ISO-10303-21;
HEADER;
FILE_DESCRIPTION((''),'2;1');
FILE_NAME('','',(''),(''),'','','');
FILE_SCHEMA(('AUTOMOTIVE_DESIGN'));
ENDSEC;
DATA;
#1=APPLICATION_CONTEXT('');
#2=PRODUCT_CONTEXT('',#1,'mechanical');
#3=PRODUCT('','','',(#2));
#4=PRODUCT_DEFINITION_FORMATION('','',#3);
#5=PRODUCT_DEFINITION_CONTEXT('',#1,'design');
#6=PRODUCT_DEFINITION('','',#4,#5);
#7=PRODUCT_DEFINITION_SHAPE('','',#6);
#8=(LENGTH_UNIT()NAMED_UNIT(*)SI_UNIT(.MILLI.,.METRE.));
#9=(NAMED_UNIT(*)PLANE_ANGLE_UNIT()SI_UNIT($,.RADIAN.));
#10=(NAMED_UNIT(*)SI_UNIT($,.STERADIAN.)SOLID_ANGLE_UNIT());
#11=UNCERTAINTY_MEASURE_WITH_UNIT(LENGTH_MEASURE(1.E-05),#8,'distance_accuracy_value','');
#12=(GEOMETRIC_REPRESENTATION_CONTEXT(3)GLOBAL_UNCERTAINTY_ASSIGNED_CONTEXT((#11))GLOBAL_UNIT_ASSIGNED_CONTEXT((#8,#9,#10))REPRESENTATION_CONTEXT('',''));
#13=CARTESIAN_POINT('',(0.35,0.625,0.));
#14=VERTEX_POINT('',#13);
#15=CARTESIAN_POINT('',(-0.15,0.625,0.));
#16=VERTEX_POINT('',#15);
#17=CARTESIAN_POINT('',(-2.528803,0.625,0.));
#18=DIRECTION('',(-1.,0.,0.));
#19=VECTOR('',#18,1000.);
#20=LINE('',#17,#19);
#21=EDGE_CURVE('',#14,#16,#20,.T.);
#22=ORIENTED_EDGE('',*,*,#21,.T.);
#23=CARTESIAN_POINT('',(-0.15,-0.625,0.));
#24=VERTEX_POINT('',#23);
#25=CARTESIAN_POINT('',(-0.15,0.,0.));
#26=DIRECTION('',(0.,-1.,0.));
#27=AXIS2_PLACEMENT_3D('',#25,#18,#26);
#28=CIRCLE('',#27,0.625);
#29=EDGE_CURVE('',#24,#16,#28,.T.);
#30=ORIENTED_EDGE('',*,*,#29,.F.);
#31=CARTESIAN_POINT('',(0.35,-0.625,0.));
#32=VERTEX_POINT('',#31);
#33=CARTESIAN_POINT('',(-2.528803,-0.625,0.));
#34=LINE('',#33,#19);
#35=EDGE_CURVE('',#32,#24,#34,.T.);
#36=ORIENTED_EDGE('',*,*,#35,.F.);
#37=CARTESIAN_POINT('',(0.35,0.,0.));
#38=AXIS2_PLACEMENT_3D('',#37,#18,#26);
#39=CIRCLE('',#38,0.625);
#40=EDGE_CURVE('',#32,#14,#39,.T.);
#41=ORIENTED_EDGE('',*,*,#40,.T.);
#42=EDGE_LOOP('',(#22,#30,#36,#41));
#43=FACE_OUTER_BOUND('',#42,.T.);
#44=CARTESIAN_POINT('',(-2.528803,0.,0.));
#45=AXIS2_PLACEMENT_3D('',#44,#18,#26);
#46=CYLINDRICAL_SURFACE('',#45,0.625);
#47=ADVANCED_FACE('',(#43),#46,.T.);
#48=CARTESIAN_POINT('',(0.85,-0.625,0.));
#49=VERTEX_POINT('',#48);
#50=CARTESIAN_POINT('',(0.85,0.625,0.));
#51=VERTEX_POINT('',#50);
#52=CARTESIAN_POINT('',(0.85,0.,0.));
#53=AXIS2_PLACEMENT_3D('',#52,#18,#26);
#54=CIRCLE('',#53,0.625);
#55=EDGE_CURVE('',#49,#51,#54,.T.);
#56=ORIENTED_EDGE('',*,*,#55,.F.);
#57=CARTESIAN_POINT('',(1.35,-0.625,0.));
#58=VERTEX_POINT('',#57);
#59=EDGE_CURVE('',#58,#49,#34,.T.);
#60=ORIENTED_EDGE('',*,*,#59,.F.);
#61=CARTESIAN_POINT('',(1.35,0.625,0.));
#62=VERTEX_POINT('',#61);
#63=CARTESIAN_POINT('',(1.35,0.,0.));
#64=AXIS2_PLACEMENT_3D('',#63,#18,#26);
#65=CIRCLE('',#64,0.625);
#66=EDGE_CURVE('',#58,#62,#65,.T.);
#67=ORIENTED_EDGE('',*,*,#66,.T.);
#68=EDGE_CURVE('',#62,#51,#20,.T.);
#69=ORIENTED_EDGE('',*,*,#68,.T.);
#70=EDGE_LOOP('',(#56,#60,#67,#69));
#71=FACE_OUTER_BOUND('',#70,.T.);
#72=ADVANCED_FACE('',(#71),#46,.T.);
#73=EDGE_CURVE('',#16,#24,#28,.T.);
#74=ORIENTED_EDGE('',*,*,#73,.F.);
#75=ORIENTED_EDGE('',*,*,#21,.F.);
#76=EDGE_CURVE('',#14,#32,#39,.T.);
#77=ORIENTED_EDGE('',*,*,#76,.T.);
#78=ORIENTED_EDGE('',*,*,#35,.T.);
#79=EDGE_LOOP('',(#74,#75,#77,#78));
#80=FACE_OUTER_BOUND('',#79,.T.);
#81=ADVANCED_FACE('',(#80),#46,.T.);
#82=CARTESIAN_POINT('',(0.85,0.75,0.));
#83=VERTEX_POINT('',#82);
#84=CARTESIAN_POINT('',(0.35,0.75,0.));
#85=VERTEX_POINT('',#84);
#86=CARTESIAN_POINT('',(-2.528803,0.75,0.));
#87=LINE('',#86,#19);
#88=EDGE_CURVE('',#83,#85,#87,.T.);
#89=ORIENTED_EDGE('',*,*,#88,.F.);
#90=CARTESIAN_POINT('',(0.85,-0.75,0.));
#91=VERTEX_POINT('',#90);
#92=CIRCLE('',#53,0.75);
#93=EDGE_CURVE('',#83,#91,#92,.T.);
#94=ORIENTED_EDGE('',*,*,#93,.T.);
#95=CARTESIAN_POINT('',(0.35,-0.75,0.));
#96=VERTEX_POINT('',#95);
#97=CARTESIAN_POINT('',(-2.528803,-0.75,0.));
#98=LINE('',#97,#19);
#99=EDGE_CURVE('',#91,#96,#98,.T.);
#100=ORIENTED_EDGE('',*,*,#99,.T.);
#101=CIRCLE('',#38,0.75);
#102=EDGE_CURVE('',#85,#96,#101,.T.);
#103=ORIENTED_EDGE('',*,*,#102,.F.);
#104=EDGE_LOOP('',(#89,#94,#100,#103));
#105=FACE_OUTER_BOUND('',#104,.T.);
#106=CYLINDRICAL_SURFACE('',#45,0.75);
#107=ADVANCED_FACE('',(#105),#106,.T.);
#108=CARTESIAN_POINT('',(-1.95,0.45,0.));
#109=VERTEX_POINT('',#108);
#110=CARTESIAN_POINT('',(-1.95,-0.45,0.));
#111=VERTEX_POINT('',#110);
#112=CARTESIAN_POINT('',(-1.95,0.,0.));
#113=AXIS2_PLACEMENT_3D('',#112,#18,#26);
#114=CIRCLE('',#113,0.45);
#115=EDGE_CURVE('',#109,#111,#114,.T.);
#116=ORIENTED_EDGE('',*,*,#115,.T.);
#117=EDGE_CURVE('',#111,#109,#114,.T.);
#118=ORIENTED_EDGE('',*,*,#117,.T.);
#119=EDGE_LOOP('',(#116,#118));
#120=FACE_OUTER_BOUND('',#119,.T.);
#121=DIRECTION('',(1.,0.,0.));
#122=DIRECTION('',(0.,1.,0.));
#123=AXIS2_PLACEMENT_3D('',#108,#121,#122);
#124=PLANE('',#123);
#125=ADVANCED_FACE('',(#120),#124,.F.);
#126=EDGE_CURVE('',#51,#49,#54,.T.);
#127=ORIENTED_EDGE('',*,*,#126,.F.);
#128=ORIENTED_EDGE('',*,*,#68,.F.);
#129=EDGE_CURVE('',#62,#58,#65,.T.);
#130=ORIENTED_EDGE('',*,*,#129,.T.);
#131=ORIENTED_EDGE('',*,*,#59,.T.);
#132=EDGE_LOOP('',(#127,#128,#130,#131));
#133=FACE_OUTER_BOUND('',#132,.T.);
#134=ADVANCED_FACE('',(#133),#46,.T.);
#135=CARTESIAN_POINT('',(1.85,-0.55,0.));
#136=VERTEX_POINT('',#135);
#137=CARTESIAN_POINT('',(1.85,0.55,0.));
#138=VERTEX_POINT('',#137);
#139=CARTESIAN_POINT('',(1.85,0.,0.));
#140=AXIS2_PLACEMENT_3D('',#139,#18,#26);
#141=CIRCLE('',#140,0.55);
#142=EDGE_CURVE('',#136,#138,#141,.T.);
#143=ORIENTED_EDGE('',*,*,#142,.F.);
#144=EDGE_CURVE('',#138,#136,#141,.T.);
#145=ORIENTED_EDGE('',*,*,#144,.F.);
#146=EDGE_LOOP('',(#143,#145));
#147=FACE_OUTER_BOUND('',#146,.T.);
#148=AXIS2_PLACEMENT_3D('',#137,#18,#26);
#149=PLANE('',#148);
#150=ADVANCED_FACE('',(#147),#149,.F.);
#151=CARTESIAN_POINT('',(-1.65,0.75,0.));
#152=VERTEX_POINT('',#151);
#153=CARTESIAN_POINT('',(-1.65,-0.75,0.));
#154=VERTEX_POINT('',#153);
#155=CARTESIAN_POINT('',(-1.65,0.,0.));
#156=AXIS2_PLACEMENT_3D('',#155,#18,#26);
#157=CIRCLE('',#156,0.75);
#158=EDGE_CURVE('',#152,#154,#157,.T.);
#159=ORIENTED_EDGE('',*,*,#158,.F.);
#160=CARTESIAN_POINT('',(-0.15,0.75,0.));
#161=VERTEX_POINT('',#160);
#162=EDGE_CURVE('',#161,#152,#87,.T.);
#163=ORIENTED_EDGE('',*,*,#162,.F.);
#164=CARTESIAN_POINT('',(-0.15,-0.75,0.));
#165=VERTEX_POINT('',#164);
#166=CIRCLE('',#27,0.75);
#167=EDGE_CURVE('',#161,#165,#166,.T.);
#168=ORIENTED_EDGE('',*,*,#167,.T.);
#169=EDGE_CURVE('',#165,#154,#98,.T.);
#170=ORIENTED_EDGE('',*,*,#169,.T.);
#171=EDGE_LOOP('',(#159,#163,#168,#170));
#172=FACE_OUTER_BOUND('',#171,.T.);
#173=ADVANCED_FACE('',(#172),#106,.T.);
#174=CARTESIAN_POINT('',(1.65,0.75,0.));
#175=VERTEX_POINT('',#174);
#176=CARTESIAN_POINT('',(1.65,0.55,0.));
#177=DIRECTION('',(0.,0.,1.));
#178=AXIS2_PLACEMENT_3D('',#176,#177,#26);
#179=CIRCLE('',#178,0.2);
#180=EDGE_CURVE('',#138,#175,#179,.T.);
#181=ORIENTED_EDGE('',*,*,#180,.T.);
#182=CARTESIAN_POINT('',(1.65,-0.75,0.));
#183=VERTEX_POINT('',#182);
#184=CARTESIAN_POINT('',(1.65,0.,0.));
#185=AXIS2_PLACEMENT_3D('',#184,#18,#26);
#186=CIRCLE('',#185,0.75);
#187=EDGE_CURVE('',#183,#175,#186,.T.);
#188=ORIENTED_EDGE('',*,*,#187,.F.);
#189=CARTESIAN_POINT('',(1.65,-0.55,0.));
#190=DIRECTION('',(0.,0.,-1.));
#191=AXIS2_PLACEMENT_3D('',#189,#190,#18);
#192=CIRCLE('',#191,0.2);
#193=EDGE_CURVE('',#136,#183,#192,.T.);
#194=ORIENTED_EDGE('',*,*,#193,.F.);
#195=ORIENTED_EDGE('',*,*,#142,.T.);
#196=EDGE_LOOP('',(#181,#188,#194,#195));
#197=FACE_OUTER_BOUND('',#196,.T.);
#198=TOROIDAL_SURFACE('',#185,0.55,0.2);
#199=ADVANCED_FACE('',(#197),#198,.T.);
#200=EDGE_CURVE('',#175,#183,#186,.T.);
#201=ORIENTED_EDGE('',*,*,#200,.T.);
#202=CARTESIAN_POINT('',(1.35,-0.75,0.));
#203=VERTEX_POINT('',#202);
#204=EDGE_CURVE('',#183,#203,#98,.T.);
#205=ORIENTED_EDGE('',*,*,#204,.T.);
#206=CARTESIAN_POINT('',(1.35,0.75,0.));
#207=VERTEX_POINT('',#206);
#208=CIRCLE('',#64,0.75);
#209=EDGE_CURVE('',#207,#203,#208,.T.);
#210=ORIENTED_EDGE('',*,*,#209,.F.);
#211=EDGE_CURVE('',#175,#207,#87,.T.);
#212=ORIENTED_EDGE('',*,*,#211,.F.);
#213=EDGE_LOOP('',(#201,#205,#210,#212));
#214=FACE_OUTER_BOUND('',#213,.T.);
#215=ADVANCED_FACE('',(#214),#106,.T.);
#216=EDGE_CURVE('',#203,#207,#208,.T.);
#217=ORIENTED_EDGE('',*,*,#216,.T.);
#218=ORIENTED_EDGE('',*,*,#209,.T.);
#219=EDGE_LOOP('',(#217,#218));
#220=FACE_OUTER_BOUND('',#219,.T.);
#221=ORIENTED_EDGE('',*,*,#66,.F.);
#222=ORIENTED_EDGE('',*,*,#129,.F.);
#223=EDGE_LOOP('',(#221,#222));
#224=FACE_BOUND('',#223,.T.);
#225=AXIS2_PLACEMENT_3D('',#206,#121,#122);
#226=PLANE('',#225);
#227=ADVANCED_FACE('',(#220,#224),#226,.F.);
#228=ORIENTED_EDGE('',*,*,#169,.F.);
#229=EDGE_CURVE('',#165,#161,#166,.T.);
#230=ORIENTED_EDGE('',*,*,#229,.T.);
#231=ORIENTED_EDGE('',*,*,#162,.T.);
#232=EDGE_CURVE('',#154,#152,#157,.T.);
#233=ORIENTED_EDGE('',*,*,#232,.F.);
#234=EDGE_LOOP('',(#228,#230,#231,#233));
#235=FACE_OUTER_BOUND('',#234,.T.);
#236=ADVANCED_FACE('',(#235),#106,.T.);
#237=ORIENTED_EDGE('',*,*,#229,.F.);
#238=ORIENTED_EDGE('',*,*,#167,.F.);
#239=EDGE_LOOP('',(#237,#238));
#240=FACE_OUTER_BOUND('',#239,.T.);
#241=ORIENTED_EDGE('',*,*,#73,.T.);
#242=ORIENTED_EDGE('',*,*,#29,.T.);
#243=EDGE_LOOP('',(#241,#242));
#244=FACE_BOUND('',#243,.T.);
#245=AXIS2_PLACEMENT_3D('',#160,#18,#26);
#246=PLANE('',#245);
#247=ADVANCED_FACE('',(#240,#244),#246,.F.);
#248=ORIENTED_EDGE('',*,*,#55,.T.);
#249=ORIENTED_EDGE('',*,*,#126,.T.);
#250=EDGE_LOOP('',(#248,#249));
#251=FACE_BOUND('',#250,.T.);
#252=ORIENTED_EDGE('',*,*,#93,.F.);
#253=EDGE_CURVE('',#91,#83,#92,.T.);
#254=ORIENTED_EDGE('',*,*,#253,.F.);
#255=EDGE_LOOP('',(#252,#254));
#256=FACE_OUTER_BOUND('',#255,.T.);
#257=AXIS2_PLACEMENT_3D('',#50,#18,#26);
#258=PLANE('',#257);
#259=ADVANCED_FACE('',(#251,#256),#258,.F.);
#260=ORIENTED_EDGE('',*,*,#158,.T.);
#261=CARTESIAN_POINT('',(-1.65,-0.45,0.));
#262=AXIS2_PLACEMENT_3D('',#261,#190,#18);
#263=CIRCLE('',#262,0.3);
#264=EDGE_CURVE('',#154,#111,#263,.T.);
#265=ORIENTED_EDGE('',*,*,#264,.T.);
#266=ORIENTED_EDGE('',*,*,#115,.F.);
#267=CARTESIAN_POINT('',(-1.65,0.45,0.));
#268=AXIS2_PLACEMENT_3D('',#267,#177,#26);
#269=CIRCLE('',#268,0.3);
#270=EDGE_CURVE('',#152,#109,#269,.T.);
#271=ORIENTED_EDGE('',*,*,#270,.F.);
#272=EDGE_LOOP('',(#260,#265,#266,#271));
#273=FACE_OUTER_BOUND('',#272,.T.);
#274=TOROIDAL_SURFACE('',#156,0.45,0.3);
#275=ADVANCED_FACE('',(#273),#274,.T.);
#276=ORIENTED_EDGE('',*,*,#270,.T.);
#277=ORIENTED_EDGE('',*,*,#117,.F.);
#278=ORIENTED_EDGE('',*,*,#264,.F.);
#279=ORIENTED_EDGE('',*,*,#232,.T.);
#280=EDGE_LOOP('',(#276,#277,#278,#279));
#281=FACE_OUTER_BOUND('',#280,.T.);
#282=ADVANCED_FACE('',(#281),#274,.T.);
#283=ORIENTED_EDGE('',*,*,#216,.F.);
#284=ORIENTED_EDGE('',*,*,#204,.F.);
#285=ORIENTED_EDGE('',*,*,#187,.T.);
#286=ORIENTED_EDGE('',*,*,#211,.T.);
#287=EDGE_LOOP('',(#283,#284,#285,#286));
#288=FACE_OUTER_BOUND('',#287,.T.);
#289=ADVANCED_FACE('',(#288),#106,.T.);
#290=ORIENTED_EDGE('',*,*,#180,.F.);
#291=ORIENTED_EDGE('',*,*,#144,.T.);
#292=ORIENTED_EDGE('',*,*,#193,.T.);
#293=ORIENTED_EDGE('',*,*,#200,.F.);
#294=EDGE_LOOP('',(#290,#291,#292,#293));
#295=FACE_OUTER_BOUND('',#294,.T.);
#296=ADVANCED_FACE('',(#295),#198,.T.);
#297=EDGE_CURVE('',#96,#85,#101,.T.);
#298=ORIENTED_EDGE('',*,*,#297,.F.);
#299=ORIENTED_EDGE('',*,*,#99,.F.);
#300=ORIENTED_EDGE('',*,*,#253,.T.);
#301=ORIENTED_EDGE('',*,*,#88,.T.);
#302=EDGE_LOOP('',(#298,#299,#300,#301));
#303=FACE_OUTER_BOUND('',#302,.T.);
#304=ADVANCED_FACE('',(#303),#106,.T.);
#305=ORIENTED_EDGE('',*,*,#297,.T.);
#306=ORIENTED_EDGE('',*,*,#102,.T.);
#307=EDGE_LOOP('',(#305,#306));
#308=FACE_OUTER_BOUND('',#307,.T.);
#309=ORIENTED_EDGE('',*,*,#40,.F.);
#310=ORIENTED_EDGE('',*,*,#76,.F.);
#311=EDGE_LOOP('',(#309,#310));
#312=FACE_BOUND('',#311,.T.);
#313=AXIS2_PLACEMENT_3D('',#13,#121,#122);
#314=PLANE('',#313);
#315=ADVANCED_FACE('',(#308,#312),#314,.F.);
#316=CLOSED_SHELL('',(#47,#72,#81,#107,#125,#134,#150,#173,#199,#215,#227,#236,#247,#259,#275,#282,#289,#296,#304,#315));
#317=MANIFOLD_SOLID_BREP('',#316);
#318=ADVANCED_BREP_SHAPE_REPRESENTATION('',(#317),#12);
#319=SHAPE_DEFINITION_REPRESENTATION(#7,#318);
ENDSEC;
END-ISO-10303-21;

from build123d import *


with BuildPart() as part:
    # 草图1 → 旋转1 (revolve)
    with BuildSketch(Plane.XY, mode=Mode.PRIVATE) as revolve_1_sk:
        with BuildLine():
            Line((1.35, 0.75), (1.35, 0.625))
            Line((1.35, 0.625), (0.85, 0.625))
            Line((0.85, 0.625), (0.85, 0.75))
            Line((0.85, 0.75), (0.35, 0.75))
            Line((0.35, 0.75), (0.35, 0.625))
            Line((0.35, 0.625), (-0.15, 0.625))
            Line((-0.15, 0.625), (-0.15, 0.75))
            Line((-0.15, 0.75), (-1.65, 0.75))
            ThreePointArc((-1.65, 0.75), (-1.862132034, 0.662132034), (-1.95, 0.45))
            Line((-1.95, 0.45), (-1.95, 0))
            Line((-1.95, 0), (1.85, 0))
            Line((1.85, 0), (1.85, 0.55))
            ThreePointArc((1.85, 0.55), (1.791421356, 0.691421356), (1.65, 0.75))
            Line((1.65, 0.75), (1.35, 0.75))
        make_face()
    revolve(revolve_1_sk.sketch.rotate(Axis((-2.528803116, 0, 0), (1, 0, 0)), 180), axis=Axis((-2.528803116, 0, 0), (1, 0, 0)))


solid = part.part
